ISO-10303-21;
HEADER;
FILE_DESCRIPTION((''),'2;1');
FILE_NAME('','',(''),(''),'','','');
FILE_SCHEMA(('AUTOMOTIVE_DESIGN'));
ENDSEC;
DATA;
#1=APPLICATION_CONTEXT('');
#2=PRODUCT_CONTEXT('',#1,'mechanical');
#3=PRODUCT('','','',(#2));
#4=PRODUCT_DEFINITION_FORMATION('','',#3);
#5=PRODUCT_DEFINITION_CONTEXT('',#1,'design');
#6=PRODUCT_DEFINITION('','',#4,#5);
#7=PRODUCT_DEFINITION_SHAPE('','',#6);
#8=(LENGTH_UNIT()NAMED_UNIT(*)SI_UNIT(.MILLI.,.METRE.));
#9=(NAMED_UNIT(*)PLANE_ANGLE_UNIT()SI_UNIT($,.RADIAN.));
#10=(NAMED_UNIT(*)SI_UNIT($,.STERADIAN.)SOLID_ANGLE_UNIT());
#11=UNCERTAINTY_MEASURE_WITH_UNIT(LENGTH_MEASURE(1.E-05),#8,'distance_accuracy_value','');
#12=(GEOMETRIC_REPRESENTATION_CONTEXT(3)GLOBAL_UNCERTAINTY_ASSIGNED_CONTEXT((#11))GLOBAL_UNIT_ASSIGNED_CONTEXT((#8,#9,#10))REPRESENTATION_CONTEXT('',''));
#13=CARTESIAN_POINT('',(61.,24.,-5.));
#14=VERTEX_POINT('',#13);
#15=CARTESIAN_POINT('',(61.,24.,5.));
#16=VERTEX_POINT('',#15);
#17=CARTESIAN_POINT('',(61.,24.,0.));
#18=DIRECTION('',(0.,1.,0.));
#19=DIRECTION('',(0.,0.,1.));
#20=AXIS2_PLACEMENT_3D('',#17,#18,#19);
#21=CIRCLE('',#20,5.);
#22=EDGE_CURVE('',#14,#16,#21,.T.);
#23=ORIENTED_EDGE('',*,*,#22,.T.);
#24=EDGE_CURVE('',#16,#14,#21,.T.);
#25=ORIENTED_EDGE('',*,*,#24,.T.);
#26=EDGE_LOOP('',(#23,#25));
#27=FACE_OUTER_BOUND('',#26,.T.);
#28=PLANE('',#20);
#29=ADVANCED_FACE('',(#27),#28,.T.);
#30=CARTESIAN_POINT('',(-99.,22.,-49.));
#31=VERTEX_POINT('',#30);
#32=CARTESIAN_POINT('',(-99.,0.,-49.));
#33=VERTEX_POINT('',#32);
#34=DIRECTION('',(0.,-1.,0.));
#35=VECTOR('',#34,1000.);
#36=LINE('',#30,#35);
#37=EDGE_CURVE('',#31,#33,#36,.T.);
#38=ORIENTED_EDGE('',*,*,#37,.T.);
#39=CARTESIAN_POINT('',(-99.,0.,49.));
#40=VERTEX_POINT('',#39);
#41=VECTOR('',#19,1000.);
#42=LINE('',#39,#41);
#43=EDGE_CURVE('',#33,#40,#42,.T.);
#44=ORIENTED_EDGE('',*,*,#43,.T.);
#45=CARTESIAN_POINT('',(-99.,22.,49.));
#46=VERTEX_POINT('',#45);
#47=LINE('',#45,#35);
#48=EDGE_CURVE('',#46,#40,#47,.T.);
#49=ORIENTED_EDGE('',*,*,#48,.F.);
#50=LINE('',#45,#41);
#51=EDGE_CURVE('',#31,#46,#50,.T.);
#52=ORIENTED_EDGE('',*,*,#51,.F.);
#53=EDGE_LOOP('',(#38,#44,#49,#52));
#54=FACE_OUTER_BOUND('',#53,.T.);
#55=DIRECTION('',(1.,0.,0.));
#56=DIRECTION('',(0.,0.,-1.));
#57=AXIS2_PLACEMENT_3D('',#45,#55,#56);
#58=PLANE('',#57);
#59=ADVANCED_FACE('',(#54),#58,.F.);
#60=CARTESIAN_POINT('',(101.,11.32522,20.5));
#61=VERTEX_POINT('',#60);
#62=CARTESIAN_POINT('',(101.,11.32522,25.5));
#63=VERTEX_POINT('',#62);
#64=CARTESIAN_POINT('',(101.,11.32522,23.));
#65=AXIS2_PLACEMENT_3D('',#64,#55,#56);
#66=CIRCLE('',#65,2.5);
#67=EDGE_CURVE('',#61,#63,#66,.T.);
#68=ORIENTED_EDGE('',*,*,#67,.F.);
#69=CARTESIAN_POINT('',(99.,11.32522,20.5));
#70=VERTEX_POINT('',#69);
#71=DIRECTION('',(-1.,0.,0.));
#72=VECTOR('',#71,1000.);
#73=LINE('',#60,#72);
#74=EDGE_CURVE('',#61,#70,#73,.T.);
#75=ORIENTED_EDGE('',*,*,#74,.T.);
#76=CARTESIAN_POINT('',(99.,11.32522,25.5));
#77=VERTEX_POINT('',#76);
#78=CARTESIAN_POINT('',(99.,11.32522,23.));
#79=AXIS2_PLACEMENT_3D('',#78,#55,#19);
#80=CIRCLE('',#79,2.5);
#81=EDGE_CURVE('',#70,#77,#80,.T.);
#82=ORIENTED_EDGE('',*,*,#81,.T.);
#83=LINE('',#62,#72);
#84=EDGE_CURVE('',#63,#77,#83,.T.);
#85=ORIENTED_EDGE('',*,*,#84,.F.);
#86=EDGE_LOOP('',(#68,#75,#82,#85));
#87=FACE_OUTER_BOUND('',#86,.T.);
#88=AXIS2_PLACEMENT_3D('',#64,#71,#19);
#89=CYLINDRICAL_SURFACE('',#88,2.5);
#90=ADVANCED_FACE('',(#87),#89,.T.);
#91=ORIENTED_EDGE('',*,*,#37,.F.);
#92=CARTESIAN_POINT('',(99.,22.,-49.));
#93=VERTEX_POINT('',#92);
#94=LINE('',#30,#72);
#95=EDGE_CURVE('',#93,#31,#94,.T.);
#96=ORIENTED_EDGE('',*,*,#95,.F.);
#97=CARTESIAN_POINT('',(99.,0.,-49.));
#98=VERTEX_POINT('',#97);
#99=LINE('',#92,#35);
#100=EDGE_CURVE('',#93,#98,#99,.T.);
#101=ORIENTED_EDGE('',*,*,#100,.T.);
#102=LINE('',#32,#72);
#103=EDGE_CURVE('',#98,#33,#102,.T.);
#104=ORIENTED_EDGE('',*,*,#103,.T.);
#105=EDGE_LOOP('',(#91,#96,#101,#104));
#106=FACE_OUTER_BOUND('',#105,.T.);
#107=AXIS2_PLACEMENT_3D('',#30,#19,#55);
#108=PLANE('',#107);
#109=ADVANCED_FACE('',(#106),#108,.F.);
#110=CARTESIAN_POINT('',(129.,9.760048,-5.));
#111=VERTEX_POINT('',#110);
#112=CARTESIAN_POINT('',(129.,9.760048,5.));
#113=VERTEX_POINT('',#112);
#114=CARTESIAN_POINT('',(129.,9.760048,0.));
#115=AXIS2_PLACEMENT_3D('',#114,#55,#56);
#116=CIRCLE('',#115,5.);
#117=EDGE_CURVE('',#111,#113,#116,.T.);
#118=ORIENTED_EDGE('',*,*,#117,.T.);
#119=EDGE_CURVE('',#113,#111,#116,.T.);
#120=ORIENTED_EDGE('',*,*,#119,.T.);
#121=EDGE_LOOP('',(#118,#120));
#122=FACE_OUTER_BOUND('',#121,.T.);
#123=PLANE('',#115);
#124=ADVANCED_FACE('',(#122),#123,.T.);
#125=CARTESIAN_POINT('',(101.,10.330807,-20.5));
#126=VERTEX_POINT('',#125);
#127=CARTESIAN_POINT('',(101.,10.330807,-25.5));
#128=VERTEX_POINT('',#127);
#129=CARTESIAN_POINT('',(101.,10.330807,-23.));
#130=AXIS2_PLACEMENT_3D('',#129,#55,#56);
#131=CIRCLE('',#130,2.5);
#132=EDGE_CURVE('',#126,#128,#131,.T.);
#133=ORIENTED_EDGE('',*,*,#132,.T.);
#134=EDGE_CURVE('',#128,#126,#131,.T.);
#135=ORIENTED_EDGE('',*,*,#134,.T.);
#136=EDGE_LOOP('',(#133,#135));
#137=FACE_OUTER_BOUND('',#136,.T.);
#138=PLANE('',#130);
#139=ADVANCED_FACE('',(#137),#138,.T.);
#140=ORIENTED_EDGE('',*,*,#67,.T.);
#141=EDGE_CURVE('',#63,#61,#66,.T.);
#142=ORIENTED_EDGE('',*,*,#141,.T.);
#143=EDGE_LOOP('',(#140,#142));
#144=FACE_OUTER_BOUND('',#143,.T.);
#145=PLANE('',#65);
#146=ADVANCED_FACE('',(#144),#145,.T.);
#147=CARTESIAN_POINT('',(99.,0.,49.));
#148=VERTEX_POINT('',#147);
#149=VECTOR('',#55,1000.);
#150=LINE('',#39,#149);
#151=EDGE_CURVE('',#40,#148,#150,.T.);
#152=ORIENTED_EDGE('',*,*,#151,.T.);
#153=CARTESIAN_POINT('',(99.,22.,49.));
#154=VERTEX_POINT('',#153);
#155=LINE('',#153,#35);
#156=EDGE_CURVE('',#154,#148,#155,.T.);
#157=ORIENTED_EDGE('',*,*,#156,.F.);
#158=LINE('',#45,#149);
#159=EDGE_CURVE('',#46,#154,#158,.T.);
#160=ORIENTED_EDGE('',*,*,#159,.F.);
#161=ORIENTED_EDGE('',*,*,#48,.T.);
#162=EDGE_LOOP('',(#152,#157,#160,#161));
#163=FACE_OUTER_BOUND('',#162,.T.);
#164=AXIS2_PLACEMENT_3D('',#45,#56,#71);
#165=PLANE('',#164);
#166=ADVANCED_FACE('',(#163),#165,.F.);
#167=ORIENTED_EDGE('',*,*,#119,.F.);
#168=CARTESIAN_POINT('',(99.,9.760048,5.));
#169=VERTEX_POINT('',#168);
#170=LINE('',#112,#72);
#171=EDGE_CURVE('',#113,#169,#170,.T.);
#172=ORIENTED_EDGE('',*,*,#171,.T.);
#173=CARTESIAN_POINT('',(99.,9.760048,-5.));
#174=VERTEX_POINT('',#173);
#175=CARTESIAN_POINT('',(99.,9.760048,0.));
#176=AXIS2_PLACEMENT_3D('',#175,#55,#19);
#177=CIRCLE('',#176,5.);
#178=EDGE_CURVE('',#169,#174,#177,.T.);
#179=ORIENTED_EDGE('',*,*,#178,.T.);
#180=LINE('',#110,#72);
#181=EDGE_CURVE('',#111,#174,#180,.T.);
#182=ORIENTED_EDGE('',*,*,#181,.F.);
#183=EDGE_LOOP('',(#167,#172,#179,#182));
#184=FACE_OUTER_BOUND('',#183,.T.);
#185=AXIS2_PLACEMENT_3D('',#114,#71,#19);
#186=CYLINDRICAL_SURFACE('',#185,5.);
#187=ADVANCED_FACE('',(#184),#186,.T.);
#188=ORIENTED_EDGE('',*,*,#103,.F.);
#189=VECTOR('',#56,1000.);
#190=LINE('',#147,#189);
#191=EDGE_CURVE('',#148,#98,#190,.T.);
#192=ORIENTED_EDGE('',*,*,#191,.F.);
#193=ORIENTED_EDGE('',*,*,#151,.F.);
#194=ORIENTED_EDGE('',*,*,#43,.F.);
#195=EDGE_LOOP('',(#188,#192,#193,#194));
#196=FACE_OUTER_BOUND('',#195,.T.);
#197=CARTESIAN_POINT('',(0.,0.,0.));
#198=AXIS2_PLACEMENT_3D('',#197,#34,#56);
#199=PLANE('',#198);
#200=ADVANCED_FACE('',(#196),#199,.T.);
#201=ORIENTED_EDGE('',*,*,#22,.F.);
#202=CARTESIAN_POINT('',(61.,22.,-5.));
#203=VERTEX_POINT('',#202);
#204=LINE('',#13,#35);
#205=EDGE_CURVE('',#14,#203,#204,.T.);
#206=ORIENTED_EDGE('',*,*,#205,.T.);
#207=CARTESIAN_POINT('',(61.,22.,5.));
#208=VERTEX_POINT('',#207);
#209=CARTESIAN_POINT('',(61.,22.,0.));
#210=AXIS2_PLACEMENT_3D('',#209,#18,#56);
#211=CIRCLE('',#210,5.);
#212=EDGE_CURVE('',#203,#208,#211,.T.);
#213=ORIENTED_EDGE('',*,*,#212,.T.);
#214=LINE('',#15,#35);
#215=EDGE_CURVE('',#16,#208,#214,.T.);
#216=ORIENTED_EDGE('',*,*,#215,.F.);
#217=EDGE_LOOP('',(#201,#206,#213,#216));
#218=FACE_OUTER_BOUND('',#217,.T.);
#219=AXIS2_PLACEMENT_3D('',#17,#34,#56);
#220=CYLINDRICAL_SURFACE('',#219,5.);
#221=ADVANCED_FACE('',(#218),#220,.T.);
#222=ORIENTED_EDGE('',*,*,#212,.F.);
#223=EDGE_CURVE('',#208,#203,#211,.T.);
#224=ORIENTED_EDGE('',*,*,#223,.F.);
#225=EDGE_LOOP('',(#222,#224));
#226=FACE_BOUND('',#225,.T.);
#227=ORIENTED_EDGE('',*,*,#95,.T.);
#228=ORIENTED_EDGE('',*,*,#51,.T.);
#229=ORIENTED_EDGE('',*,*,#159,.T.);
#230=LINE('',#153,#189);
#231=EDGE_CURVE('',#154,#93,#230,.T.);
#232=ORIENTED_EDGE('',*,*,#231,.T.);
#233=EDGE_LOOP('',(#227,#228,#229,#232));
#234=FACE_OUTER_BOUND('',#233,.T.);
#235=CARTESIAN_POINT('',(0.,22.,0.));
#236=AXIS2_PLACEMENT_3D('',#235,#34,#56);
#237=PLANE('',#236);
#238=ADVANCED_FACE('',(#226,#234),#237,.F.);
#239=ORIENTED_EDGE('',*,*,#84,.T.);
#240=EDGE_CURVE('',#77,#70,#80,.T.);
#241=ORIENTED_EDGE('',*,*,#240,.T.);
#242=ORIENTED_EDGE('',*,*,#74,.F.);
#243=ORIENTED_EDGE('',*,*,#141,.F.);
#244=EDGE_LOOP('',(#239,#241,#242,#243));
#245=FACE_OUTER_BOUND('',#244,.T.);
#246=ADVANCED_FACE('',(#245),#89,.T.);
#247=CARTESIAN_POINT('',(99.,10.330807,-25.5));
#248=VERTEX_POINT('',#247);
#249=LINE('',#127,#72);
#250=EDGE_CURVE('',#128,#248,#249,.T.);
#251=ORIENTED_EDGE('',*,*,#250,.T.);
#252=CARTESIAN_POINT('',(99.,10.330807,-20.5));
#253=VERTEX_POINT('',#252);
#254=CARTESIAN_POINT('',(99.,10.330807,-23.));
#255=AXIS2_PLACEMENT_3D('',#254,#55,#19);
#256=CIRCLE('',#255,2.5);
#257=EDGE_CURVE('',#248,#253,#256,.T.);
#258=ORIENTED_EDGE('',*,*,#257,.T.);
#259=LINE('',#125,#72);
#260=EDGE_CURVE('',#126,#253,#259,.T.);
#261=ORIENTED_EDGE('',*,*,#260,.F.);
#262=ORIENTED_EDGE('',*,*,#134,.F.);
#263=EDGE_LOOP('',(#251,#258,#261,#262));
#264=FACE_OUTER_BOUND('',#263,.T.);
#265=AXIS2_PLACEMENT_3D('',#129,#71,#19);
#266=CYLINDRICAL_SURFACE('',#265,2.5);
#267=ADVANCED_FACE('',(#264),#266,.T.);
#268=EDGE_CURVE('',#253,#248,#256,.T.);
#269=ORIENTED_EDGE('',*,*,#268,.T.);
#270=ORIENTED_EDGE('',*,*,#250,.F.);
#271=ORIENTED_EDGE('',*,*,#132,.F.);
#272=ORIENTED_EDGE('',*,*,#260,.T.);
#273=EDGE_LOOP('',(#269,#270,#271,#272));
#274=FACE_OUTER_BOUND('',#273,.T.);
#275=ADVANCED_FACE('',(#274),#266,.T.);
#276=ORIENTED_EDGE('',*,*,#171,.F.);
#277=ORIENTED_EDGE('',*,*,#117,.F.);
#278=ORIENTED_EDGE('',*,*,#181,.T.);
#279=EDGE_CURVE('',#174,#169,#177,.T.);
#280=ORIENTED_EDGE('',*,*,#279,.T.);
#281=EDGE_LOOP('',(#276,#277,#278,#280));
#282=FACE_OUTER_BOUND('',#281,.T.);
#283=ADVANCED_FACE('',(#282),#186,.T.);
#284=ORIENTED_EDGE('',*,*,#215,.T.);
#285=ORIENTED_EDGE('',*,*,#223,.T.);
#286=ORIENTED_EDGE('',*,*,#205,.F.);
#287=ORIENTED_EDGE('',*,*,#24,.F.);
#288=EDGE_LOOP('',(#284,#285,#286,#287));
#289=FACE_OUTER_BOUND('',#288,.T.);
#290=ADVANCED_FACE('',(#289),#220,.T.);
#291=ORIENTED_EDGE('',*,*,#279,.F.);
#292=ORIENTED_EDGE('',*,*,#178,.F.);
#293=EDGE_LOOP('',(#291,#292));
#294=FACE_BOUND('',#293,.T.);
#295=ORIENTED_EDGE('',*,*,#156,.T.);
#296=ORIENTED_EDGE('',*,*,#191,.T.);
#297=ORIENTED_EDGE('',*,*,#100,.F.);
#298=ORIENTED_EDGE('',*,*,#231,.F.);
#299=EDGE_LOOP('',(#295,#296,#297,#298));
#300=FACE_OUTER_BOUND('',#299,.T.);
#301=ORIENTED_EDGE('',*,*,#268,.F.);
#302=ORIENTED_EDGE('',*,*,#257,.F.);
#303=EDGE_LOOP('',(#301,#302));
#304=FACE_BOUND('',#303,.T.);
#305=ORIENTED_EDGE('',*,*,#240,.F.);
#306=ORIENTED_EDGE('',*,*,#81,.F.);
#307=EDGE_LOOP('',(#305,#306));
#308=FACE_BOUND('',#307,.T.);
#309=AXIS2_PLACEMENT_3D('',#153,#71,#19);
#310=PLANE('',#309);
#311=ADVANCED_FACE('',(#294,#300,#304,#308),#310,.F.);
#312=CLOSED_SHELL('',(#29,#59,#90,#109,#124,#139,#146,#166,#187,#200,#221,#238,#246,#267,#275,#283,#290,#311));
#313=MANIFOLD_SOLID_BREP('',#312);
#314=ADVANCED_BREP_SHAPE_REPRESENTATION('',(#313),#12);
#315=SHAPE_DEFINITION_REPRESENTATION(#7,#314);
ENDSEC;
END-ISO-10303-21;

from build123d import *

# Parameters (mm, degrees)
SKETCH1_W           = 198
SKETCH1_H           = 98
BOSS_EXTRUDE1_DEPTH = 22
SKETCH2_R           = 5
BOSS_EXTRUDE2_DEPTH = 30
SKETCH3_R           = 5
BOSS_EXTRUDE3_DEPTH = 2
SKETCH4_R           = 2.5
BOSS_EXTRUDE4_DEPTH = 2


with BuildPart() as part:
    # Sketch1 → Boss-Extrude1 (new body)
    with BuildSketch(Plane(origin=(0, 0, 0), x_dir=(1, 0, 0), z_dir=(0, 1, 0))):
        Rectangle(SKETCH1_W, SKETCH1_H)
    extrude(amount=BOSS_EXTRUDE1_DEPTH)

    # Sketch2 → Boss-Extrude2 (add)
    with BuildSketch(Plane(origin=(99, 0, 0), x_dir=(0, 0, -1), z_dir=(1, 0, 0))):
        with Locations(Location((0, 9.760048185, 0), (0, 0, 180))):
            Circle(SKETCH2_R)
    extrude(amount=BOSS_EXTRUDE2_DEPTH)

    # Sketch3 → Boss-Extrude3 (add)
    with BuildSketch(Plane(origin=(0, 22, 0), x_dir=(1, 0, 0), z_dir=(0, 1, 0))):
        with Locations(Location((61, 0, 0), (0, 0, 90))):
            Circle(SKETCH3_R)
    extrude(amount=BOSS_EXTRUDE3_DEPTH)

    # Sketch4 → Boss-Extrude4 (add)
    with BuildSketch(Plane(origin=(99, 0, 0), x_dir=(0, 0, -1), z_dir=(1, 0, 0))):
        with Locations(Location((23, 10.330807158, 0), (0, 0, 180))):
            Circle(SKETCH4_R)
        with Locations(Location((-23, 11.325219915, 0), (0, 0, 180))):
            Circle(SKETCH4_R)
    extrude(amount=BOSS_EXTRUDE4_DEPTH)


solid = part.part
